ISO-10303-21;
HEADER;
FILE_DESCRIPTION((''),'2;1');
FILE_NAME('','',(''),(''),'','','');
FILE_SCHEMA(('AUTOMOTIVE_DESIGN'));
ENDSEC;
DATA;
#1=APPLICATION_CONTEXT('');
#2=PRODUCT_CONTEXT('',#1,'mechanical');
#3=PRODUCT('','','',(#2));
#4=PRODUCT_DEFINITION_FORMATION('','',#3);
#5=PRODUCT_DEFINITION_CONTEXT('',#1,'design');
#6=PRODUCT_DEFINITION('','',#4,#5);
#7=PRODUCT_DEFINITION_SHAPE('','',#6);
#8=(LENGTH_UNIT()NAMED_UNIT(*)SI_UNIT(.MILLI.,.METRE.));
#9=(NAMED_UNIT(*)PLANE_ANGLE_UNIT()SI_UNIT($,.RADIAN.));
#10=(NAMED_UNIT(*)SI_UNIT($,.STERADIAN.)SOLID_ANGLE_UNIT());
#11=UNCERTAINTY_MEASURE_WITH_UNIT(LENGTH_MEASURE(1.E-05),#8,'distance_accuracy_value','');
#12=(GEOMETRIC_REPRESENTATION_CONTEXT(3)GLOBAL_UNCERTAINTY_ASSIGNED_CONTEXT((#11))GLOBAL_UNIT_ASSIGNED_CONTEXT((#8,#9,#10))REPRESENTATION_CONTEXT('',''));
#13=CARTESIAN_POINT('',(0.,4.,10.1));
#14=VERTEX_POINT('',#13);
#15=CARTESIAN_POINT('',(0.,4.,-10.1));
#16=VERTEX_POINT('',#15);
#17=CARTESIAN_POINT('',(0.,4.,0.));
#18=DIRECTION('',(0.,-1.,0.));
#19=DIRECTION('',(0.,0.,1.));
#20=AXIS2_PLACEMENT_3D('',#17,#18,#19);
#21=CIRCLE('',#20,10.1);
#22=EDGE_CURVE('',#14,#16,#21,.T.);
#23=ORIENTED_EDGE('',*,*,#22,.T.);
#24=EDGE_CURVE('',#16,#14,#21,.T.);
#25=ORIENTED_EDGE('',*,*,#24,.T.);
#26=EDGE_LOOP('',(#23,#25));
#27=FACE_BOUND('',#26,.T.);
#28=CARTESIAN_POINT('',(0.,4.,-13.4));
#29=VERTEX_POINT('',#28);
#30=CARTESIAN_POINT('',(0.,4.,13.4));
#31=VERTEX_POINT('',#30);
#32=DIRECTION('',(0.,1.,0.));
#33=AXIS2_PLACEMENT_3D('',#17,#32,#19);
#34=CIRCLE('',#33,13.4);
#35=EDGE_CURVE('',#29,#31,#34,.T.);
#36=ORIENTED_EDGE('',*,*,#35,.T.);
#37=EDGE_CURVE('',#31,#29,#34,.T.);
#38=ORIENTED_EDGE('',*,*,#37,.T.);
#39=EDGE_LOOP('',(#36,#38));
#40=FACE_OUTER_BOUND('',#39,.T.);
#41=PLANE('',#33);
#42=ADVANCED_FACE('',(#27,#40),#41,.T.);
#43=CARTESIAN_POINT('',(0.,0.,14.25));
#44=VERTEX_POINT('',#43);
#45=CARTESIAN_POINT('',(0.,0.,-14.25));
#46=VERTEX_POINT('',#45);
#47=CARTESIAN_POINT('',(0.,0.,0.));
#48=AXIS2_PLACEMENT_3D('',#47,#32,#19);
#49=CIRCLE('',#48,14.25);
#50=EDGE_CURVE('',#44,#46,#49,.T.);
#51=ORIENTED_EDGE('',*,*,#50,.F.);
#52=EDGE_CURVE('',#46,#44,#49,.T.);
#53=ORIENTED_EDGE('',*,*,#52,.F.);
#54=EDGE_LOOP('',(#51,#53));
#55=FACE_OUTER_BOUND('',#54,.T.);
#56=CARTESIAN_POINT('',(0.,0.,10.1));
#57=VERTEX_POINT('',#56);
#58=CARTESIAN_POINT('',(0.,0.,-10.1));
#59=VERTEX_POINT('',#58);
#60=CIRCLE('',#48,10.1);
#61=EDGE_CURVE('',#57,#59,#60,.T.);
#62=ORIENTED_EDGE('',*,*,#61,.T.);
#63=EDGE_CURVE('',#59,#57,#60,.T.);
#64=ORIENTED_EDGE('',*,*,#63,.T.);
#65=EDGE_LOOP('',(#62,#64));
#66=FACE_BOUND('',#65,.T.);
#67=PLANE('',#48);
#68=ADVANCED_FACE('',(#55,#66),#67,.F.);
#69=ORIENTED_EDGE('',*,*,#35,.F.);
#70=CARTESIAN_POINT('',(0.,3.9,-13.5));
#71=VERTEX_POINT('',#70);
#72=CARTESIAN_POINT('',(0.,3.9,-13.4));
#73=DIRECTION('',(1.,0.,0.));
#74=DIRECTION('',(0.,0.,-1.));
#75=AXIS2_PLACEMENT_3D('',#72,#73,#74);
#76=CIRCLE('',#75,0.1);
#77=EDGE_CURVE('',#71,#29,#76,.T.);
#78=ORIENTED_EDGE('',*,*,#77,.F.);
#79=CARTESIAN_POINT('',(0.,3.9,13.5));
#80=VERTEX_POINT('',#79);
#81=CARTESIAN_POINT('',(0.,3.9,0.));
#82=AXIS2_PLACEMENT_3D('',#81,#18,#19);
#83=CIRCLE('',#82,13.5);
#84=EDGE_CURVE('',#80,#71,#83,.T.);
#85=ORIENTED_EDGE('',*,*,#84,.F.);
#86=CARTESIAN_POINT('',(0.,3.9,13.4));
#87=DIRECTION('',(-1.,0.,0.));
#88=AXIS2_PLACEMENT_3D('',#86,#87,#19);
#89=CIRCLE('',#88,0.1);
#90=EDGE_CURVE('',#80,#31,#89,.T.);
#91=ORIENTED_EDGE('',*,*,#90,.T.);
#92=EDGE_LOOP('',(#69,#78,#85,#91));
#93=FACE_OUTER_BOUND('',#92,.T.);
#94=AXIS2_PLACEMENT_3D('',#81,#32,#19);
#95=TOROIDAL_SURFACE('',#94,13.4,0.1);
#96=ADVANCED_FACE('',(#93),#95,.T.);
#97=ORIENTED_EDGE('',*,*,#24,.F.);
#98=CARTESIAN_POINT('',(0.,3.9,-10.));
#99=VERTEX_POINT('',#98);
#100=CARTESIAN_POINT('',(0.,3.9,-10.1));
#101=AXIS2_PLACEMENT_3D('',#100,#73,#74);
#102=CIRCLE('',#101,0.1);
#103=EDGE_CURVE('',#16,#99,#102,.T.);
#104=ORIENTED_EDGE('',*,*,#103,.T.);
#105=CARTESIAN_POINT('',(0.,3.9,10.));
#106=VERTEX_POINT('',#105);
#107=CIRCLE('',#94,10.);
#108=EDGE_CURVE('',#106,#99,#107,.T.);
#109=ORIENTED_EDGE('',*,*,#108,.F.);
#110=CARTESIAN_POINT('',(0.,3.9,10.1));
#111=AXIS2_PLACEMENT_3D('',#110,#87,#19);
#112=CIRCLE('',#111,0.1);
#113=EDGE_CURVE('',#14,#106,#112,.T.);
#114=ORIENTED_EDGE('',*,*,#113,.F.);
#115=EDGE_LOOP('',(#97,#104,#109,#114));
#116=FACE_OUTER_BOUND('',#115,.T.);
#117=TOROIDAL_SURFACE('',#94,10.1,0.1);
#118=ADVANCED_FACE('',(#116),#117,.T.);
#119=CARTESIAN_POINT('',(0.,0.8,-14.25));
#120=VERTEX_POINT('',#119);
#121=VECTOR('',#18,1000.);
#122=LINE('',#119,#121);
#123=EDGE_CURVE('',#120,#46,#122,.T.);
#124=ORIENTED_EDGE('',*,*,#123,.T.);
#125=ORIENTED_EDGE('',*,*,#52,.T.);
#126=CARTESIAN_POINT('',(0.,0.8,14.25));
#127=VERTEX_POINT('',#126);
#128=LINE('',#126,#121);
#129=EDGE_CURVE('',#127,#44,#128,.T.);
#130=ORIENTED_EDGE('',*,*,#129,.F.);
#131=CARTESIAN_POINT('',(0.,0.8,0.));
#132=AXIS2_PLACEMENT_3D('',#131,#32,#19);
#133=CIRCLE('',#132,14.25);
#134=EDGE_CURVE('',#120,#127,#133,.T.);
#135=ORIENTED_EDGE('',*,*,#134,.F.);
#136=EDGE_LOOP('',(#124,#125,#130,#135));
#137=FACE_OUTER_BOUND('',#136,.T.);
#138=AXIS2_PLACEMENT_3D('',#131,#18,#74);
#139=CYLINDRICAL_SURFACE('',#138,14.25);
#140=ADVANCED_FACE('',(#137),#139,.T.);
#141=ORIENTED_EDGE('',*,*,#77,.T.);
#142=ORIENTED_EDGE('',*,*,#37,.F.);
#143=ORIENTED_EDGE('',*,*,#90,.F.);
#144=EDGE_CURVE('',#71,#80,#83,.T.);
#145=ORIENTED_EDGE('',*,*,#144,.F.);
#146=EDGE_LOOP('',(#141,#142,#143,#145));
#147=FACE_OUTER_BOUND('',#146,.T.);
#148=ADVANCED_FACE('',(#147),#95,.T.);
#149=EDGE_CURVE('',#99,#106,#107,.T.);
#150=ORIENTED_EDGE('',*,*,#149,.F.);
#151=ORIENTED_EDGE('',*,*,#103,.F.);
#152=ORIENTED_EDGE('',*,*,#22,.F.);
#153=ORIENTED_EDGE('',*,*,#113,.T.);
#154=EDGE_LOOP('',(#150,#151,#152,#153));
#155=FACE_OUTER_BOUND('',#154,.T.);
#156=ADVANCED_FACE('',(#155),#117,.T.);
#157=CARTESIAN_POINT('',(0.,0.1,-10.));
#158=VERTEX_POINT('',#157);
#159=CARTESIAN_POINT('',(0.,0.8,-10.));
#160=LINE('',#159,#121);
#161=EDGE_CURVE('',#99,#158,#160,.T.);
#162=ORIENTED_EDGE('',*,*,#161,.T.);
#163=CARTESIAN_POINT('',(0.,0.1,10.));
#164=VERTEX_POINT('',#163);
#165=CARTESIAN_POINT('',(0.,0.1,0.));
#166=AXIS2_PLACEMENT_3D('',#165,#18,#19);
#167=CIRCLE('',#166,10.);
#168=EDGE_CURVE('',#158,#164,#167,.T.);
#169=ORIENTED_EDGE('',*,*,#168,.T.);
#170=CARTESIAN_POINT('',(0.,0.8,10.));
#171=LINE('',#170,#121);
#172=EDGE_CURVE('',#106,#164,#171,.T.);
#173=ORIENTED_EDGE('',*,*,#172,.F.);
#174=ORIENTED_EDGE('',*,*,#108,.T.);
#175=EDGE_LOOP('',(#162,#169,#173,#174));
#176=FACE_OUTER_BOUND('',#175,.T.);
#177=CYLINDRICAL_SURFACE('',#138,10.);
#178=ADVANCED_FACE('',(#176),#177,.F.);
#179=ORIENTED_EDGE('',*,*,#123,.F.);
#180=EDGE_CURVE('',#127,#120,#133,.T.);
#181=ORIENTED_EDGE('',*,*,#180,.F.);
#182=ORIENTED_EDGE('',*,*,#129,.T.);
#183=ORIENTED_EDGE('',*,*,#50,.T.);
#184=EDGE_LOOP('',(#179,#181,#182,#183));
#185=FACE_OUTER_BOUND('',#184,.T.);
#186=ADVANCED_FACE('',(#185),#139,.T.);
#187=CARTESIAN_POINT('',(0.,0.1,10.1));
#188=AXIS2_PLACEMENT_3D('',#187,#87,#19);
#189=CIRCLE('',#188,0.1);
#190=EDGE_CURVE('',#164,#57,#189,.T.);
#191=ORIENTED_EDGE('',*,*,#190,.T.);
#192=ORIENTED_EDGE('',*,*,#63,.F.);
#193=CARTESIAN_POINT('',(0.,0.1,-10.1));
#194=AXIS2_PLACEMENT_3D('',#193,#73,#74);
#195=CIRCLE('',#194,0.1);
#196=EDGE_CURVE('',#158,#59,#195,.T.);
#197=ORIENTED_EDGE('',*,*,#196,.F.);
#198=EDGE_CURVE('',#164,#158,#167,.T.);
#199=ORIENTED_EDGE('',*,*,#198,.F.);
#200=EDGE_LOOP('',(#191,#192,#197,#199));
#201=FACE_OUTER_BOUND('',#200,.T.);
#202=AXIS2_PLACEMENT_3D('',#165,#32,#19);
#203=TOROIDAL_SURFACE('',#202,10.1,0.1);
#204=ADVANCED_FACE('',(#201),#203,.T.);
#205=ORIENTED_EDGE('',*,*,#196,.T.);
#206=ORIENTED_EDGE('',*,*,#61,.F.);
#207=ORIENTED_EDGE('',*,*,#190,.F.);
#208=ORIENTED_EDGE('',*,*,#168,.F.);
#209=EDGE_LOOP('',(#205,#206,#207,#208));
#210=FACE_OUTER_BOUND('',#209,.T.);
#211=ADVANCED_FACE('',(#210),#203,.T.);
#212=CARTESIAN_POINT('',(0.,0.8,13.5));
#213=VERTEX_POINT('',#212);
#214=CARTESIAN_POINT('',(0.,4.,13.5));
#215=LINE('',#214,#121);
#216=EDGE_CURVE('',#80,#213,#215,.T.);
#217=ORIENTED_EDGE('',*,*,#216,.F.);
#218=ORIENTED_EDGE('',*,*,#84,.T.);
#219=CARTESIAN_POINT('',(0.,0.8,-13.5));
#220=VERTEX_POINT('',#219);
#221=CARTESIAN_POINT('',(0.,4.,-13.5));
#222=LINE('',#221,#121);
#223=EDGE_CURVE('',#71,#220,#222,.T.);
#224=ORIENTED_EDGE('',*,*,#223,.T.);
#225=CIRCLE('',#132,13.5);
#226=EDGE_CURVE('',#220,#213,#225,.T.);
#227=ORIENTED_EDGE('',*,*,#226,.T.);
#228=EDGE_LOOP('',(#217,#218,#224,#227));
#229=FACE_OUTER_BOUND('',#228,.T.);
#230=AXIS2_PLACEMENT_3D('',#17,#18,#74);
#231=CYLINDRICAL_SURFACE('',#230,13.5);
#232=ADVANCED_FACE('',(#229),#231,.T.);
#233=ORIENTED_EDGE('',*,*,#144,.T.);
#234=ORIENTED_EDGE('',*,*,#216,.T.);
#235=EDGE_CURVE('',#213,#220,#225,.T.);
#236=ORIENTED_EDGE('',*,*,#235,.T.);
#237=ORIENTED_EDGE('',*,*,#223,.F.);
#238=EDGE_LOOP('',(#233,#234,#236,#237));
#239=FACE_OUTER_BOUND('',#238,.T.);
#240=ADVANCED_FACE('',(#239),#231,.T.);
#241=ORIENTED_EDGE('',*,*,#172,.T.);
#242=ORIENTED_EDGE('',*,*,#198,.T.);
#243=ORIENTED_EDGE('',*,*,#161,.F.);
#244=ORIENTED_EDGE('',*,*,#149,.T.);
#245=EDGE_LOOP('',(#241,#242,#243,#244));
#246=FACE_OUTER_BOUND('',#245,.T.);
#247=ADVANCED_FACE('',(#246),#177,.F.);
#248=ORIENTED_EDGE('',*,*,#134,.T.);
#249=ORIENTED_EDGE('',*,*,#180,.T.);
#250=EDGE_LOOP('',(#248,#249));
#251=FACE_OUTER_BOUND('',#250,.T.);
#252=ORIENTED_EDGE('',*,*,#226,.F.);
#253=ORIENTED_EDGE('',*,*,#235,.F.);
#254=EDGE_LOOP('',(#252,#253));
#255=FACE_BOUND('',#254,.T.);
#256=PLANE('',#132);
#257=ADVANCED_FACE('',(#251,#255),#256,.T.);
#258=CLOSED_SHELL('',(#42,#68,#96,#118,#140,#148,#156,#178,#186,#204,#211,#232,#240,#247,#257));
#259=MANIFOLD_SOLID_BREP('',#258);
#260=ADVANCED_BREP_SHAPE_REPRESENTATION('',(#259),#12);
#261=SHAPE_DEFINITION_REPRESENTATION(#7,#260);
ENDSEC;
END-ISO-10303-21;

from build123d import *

# Parameters (mm, degrees)
SKETCH_1_R      = 14.25
SKETCH_1_R_2    = 10
EXTRUDE_1_DEPTH = 0.8
SKETCH_2_R      = 13.5
SKETCH_2_R_2    = 10
EXTRUDE_2_DEPTH = 3.2
FILLET_R0_1_1_R = 0.1


with BuildPart() as part:
    # 草图1 → 凸台-拉伸1 (new body)
    with BuildSketch(Plane(origin=(0, 0, 0), x_dir=(1, 0, 0), z_dir=(0, 1, 0))):
        with Locations(Location((0, 0, 0), (0, 0, 270))):
            Circle(SKETCH_1_R)
        with Locations(Location((0, 0, 0), (0, 0, 270))):
            Circle(SKETCH_1_R_2, mode=Mode.SUBTRACT)
    extrude(amount=EXTRUDE_1_DEPTH)

    # 草图2 → 凸台-拉伸2 (add)
    with BuildSketch(Plane(origin=(0, 0.8, 0), x_dir=(1, 0, 0), z_dir=(0, 1, 0))):
        with Locations(Location((0, 0, 0), (0, 0, 270))):
            Circle(SKETCH_2_R)
        with Locations(Location((0, 0, 0), (0, 0, 270))):
            Circle(SKETCH_2_R_2, mode=Mode.SUBTRACT)
    extrude(amount=EXTRUDE_2_DEPTH)

    # R0.1 圆角1
    fillet_r0_1_1_edges = [part.edges().sort_by_distance(p)[0] for p in [
        (0, 4, -13.5),
        (0, 4, -10),
        (0, 0, -10),
    ]]
    fillet(fillet_r0_1_1_edges, radius=FILLET_R0_1_1_R)


solid = part.part
